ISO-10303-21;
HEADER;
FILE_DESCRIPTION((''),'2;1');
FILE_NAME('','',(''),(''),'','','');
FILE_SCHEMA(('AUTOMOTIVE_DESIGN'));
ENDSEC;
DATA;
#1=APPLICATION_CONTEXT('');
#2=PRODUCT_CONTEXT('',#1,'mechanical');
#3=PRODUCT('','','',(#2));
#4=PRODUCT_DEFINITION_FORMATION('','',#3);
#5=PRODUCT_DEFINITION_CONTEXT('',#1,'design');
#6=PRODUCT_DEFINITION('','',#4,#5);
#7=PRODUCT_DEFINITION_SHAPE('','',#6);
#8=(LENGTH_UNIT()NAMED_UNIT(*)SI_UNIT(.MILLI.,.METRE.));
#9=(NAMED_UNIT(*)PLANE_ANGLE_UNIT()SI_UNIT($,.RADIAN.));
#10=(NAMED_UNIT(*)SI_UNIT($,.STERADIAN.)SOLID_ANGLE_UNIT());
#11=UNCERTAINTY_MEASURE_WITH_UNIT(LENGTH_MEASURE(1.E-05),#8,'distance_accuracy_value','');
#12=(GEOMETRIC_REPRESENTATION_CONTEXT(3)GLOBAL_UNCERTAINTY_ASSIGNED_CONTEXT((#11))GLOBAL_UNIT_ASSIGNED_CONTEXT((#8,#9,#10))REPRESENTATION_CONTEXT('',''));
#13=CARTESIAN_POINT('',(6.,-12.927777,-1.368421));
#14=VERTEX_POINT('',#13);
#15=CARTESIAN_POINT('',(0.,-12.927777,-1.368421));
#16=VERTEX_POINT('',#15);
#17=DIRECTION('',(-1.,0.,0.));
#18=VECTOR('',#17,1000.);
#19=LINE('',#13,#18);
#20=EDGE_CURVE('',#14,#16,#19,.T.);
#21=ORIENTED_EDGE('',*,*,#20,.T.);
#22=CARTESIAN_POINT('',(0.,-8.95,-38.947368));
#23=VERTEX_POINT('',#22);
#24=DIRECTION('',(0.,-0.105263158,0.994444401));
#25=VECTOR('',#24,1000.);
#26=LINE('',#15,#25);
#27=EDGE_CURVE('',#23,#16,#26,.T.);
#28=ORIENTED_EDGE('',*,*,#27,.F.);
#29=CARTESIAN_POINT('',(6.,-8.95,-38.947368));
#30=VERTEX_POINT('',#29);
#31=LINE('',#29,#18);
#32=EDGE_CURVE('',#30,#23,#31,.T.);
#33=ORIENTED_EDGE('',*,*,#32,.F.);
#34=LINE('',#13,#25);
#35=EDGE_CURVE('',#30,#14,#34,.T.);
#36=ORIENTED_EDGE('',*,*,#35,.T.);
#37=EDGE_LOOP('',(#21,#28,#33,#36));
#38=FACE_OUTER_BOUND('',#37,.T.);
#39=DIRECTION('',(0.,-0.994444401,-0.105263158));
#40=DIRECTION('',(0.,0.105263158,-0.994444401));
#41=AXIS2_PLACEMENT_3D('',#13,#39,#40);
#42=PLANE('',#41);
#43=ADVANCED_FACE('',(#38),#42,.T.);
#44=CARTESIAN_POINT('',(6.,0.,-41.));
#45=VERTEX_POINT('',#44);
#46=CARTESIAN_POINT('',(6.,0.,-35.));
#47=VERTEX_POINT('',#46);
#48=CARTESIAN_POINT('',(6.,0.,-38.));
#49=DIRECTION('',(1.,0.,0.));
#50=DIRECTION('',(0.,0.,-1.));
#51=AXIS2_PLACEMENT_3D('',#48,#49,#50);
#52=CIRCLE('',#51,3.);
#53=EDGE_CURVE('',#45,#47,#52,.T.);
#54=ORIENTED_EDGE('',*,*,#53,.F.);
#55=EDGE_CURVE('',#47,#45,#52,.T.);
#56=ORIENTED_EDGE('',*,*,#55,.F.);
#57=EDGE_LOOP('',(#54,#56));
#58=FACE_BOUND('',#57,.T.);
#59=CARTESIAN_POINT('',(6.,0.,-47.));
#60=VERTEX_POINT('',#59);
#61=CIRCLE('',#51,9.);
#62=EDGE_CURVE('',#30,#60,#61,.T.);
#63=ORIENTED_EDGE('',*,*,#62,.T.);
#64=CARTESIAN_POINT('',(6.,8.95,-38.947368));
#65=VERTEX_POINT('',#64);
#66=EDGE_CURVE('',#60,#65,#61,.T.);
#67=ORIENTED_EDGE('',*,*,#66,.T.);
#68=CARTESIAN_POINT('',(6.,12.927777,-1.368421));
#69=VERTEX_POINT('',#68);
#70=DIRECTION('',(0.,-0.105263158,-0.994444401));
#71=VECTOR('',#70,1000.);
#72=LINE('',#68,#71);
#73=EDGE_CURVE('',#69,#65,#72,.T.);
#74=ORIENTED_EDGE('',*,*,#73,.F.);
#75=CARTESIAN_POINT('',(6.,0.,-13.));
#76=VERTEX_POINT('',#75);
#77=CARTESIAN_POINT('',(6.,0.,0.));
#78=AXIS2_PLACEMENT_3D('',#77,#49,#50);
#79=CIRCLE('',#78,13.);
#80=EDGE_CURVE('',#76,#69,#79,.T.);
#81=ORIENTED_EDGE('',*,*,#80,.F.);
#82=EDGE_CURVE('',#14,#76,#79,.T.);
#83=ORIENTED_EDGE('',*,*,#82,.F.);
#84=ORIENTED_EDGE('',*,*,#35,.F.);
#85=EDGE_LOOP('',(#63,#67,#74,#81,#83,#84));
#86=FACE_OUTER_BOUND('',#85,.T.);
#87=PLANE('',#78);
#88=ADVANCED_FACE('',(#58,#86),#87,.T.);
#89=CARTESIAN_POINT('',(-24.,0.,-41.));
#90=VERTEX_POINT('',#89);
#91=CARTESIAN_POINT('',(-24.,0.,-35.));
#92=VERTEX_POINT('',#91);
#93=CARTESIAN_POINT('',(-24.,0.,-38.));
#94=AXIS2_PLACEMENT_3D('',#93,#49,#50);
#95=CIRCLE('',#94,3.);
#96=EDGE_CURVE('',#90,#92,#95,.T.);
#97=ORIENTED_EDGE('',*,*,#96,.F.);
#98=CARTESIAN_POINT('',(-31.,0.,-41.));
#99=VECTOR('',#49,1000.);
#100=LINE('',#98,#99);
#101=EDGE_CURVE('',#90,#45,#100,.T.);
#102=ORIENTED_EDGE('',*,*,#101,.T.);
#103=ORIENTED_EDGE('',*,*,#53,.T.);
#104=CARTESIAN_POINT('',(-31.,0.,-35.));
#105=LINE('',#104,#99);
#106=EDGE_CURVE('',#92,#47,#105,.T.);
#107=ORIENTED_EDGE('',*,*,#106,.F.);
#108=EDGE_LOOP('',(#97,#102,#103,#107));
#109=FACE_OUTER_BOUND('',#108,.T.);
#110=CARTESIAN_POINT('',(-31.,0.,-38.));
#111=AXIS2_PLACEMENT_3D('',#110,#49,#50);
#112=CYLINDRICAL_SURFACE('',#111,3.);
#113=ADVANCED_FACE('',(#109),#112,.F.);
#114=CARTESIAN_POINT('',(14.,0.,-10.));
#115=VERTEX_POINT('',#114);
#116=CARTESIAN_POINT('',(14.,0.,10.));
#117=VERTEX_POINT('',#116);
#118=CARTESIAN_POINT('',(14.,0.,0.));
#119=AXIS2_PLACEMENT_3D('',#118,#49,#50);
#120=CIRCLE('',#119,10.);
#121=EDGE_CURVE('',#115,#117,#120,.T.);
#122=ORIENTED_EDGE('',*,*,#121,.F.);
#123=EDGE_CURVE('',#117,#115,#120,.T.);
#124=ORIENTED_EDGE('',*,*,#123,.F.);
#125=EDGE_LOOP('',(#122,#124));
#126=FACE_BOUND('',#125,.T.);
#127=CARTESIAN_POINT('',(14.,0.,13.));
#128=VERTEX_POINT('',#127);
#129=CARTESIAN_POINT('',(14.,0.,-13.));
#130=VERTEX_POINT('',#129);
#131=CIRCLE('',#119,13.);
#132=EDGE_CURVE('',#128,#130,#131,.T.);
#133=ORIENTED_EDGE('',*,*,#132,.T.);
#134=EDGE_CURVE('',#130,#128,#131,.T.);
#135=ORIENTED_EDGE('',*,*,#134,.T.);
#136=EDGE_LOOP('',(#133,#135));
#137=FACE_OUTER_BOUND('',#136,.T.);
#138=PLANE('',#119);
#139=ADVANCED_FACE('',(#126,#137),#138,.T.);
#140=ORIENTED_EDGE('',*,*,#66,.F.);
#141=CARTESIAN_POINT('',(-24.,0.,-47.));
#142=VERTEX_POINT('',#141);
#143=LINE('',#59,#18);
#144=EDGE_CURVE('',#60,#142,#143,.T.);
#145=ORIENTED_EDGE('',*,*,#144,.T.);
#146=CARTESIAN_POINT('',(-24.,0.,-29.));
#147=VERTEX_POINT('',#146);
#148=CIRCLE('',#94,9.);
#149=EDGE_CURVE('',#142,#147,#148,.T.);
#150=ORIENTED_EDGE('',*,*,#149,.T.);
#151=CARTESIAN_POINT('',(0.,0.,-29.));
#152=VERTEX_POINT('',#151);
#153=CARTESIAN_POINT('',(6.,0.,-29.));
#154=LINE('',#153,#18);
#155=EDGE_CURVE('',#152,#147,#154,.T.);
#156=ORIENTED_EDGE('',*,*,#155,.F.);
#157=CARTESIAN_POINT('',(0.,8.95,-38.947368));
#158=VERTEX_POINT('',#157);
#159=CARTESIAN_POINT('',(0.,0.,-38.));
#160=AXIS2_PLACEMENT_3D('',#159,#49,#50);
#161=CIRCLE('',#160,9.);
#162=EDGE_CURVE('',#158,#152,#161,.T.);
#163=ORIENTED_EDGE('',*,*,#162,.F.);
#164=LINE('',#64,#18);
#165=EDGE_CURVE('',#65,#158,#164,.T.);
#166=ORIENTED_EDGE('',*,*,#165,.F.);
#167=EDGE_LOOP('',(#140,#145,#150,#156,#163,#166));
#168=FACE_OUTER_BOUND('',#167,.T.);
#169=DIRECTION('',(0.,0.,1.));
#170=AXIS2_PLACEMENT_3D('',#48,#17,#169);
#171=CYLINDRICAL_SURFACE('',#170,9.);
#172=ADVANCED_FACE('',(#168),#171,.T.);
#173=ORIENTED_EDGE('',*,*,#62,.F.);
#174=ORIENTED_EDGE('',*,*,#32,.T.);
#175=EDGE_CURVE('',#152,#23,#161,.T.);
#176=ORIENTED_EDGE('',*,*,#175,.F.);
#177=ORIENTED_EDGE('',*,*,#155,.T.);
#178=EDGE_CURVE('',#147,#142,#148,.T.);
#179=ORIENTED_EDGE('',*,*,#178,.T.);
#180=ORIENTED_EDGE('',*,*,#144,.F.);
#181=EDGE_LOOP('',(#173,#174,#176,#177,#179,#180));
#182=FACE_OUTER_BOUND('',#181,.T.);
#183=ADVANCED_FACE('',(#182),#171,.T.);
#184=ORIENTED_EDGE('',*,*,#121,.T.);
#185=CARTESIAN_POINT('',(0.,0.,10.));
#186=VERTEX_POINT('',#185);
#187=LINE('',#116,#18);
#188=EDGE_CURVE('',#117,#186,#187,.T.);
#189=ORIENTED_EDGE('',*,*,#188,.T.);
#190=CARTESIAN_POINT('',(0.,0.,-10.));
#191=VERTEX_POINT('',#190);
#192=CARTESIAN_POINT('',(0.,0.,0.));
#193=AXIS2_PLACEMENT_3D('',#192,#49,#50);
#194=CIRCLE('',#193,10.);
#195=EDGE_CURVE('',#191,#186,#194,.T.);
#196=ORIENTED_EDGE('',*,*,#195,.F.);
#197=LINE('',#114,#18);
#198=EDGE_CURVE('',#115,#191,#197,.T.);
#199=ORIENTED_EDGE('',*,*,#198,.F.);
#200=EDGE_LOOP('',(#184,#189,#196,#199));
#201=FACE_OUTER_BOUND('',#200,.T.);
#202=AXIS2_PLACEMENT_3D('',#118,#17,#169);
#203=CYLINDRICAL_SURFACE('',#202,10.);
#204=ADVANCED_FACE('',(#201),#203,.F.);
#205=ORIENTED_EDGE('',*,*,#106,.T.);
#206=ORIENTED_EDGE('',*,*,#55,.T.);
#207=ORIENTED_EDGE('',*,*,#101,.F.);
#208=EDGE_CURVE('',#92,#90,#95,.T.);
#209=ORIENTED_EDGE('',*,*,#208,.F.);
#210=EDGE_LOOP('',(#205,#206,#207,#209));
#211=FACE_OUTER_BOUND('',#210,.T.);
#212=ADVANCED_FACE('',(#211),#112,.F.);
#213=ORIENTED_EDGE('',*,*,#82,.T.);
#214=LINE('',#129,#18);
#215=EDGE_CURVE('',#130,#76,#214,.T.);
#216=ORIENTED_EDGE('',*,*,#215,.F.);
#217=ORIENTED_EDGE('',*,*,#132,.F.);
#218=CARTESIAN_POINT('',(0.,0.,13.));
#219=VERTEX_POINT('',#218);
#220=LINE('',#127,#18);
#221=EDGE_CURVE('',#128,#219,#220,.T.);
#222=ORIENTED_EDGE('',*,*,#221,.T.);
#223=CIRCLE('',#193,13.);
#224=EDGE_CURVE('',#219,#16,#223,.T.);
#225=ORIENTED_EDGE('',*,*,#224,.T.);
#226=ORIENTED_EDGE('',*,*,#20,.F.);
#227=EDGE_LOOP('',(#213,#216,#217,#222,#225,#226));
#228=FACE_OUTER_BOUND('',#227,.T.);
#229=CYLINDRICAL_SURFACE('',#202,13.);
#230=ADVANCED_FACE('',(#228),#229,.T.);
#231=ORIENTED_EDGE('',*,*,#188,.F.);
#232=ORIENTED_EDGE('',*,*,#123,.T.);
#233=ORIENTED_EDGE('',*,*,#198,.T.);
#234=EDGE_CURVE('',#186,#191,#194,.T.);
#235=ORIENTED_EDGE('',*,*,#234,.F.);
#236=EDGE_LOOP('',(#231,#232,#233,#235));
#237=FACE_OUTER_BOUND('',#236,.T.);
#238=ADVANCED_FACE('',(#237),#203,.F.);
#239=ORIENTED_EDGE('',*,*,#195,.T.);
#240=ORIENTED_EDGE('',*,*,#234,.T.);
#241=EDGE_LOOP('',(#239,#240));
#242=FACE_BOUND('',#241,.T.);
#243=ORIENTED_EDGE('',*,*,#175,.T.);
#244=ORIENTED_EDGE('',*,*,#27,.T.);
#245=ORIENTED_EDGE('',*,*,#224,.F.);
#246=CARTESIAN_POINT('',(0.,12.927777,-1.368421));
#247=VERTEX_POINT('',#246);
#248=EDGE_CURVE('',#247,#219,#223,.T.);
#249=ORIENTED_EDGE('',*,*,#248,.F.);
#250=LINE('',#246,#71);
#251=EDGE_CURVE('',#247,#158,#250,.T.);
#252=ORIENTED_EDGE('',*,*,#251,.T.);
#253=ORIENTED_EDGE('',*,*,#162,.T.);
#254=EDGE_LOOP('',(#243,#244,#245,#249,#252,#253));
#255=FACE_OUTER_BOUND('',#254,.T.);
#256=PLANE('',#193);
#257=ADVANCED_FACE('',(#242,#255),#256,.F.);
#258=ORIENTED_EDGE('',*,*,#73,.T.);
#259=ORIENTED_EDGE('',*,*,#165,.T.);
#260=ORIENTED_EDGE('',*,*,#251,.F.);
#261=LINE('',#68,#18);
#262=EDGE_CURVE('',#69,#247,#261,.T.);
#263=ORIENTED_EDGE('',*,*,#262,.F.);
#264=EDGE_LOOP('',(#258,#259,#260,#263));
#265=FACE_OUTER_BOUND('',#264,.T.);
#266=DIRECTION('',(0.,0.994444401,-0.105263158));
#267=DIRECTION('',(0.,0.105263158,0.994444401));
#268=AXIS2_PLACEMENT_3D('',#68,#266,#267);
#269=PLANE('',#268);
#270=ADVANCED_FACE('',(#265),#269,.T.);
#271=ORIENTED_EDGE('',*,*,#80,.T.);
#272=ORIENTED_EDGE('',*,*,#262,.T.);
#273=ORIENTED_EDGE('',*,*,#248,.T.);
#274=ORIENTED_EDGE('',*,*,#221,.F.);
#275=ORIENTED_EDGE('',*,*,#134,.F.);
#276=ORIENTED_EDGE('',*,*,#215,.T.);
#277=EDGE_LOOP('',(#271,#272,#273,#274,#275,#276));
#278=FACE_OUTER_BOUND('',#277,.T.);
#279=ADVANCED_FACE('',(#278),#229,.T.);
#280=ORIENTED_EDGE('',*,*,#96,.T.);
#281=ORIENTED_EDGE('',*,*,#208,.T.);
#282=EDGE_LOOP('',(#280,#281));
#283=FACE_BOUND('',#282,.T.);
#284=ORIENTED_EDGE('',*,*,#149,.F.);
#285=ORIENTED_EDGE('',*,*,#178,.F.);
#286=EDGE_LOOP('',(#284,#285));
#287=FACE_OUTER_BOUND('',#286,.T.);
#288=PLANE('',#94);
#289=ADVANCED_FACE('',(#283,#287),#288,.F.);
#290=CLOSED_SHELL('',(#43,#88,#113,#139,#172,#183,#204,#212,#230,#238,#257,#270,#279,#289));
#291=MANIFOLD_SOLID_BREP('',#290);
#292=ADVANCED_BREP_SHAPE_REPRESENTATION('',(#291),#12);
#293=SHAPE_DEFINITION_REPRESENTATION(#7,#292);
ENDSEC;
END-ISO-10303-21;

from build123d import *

# Parameters (mm, degrees)
HUB_AND_POST_PROFILE_SKETCH_R   = 13
HUB_AND_POST_PROFILE_SKETCH_R_2 = 10
HUB_RING_26X_20_DEPTH           = 14
SKETCH1_3_R                     = 9
PIN_POST_18_DEPTH               = 24
ARM_WEB_SKETCH_R                = 9
ARM_WEB_6MM_DEPTH               = 6
PIN_HOLE_SKETCH_R               = 3
PIN_HOLE_6_DEPTH                = 37


with BuildPart() as part:
    # Hub and Post Profile Sketch → Hub Ring _26x_20 (new body)
    with BuildSketch(Plane(origin=(0, 0, 0), x_dir=(0, 0, -1), z_dir=(1, 0, 0))):
        Circle(HUB_AND_POST_PROFILE_SKETCH_R)
        Circle(HUB_AND_POST_PROFILE_SKETCH_R_2, mode=Mode.SUBTRACT)
    extrude(amount=HUB_RING_26X_20_DEPTH)



with BuildPart() as body_2:
    # Sketch1_3 → Pin Post _18 (new body)
    with BuildSketch(Plane(origin=(0, 0, 0), x_dir=(0, 0, -1), z_dir=(1, 0, 0))):
        with Locations((38, 0)):
            Circle(SKETCH1_3_R)
    extrude(amount=-PIN_POST_18_DEPTH)


with BuildPart() as part_1:
    add(part.part)

    add(body_2.part)  # Arm Web 6mm merges body 2
    # Arm Web Sketch → Arm Web 6mm (add)
    with BuildSketch(Plane(origin=(0, 0, 0), x_dir=(0, 0, -1), z_dir=(1, 0, 0))):
        with BuildLine():
            Line((38.947368421, 8.949999613), (1.368421053, 12.927777219))
            ThreePointArc((1.368421053, 12.927777219), (9.664095242, 8.695128703), (13, 0))
            ThreePointArc((13, 0), (9.664095242, -8.695128703), (1.368421053, -12.927777219))
            Line((1.368421053, -12.927777219), (38.947368421, -8.949999613))
            ThreePointArc((38.947368421, -8.949999613), (29, 0), (38.947368421, 8.949999613))
        make_face()
        with Locations(Location((38, 0, 0), (0, 0, 276.042328419))):
            Circle(ARM_WEB_SKETCH_R)
    extrude(amount=ARM_WEB_6MM_DEPTH)

    # Pin Hole Sketch → Pin Hole _6 (cut)
    with BuildSketch(Plane(origin=(6, 0, 0), x_dir=(0, 0, -1), z_dir=(1, 0, 0))):
        with Locations((38, 0)):
            Circle(PIN_HOLE_SKETCH_R)
    extrude(amount=-PIN_HOLE_6_DEPTH, mode=Mode.SUBTRACT)


solid = part_1.part
